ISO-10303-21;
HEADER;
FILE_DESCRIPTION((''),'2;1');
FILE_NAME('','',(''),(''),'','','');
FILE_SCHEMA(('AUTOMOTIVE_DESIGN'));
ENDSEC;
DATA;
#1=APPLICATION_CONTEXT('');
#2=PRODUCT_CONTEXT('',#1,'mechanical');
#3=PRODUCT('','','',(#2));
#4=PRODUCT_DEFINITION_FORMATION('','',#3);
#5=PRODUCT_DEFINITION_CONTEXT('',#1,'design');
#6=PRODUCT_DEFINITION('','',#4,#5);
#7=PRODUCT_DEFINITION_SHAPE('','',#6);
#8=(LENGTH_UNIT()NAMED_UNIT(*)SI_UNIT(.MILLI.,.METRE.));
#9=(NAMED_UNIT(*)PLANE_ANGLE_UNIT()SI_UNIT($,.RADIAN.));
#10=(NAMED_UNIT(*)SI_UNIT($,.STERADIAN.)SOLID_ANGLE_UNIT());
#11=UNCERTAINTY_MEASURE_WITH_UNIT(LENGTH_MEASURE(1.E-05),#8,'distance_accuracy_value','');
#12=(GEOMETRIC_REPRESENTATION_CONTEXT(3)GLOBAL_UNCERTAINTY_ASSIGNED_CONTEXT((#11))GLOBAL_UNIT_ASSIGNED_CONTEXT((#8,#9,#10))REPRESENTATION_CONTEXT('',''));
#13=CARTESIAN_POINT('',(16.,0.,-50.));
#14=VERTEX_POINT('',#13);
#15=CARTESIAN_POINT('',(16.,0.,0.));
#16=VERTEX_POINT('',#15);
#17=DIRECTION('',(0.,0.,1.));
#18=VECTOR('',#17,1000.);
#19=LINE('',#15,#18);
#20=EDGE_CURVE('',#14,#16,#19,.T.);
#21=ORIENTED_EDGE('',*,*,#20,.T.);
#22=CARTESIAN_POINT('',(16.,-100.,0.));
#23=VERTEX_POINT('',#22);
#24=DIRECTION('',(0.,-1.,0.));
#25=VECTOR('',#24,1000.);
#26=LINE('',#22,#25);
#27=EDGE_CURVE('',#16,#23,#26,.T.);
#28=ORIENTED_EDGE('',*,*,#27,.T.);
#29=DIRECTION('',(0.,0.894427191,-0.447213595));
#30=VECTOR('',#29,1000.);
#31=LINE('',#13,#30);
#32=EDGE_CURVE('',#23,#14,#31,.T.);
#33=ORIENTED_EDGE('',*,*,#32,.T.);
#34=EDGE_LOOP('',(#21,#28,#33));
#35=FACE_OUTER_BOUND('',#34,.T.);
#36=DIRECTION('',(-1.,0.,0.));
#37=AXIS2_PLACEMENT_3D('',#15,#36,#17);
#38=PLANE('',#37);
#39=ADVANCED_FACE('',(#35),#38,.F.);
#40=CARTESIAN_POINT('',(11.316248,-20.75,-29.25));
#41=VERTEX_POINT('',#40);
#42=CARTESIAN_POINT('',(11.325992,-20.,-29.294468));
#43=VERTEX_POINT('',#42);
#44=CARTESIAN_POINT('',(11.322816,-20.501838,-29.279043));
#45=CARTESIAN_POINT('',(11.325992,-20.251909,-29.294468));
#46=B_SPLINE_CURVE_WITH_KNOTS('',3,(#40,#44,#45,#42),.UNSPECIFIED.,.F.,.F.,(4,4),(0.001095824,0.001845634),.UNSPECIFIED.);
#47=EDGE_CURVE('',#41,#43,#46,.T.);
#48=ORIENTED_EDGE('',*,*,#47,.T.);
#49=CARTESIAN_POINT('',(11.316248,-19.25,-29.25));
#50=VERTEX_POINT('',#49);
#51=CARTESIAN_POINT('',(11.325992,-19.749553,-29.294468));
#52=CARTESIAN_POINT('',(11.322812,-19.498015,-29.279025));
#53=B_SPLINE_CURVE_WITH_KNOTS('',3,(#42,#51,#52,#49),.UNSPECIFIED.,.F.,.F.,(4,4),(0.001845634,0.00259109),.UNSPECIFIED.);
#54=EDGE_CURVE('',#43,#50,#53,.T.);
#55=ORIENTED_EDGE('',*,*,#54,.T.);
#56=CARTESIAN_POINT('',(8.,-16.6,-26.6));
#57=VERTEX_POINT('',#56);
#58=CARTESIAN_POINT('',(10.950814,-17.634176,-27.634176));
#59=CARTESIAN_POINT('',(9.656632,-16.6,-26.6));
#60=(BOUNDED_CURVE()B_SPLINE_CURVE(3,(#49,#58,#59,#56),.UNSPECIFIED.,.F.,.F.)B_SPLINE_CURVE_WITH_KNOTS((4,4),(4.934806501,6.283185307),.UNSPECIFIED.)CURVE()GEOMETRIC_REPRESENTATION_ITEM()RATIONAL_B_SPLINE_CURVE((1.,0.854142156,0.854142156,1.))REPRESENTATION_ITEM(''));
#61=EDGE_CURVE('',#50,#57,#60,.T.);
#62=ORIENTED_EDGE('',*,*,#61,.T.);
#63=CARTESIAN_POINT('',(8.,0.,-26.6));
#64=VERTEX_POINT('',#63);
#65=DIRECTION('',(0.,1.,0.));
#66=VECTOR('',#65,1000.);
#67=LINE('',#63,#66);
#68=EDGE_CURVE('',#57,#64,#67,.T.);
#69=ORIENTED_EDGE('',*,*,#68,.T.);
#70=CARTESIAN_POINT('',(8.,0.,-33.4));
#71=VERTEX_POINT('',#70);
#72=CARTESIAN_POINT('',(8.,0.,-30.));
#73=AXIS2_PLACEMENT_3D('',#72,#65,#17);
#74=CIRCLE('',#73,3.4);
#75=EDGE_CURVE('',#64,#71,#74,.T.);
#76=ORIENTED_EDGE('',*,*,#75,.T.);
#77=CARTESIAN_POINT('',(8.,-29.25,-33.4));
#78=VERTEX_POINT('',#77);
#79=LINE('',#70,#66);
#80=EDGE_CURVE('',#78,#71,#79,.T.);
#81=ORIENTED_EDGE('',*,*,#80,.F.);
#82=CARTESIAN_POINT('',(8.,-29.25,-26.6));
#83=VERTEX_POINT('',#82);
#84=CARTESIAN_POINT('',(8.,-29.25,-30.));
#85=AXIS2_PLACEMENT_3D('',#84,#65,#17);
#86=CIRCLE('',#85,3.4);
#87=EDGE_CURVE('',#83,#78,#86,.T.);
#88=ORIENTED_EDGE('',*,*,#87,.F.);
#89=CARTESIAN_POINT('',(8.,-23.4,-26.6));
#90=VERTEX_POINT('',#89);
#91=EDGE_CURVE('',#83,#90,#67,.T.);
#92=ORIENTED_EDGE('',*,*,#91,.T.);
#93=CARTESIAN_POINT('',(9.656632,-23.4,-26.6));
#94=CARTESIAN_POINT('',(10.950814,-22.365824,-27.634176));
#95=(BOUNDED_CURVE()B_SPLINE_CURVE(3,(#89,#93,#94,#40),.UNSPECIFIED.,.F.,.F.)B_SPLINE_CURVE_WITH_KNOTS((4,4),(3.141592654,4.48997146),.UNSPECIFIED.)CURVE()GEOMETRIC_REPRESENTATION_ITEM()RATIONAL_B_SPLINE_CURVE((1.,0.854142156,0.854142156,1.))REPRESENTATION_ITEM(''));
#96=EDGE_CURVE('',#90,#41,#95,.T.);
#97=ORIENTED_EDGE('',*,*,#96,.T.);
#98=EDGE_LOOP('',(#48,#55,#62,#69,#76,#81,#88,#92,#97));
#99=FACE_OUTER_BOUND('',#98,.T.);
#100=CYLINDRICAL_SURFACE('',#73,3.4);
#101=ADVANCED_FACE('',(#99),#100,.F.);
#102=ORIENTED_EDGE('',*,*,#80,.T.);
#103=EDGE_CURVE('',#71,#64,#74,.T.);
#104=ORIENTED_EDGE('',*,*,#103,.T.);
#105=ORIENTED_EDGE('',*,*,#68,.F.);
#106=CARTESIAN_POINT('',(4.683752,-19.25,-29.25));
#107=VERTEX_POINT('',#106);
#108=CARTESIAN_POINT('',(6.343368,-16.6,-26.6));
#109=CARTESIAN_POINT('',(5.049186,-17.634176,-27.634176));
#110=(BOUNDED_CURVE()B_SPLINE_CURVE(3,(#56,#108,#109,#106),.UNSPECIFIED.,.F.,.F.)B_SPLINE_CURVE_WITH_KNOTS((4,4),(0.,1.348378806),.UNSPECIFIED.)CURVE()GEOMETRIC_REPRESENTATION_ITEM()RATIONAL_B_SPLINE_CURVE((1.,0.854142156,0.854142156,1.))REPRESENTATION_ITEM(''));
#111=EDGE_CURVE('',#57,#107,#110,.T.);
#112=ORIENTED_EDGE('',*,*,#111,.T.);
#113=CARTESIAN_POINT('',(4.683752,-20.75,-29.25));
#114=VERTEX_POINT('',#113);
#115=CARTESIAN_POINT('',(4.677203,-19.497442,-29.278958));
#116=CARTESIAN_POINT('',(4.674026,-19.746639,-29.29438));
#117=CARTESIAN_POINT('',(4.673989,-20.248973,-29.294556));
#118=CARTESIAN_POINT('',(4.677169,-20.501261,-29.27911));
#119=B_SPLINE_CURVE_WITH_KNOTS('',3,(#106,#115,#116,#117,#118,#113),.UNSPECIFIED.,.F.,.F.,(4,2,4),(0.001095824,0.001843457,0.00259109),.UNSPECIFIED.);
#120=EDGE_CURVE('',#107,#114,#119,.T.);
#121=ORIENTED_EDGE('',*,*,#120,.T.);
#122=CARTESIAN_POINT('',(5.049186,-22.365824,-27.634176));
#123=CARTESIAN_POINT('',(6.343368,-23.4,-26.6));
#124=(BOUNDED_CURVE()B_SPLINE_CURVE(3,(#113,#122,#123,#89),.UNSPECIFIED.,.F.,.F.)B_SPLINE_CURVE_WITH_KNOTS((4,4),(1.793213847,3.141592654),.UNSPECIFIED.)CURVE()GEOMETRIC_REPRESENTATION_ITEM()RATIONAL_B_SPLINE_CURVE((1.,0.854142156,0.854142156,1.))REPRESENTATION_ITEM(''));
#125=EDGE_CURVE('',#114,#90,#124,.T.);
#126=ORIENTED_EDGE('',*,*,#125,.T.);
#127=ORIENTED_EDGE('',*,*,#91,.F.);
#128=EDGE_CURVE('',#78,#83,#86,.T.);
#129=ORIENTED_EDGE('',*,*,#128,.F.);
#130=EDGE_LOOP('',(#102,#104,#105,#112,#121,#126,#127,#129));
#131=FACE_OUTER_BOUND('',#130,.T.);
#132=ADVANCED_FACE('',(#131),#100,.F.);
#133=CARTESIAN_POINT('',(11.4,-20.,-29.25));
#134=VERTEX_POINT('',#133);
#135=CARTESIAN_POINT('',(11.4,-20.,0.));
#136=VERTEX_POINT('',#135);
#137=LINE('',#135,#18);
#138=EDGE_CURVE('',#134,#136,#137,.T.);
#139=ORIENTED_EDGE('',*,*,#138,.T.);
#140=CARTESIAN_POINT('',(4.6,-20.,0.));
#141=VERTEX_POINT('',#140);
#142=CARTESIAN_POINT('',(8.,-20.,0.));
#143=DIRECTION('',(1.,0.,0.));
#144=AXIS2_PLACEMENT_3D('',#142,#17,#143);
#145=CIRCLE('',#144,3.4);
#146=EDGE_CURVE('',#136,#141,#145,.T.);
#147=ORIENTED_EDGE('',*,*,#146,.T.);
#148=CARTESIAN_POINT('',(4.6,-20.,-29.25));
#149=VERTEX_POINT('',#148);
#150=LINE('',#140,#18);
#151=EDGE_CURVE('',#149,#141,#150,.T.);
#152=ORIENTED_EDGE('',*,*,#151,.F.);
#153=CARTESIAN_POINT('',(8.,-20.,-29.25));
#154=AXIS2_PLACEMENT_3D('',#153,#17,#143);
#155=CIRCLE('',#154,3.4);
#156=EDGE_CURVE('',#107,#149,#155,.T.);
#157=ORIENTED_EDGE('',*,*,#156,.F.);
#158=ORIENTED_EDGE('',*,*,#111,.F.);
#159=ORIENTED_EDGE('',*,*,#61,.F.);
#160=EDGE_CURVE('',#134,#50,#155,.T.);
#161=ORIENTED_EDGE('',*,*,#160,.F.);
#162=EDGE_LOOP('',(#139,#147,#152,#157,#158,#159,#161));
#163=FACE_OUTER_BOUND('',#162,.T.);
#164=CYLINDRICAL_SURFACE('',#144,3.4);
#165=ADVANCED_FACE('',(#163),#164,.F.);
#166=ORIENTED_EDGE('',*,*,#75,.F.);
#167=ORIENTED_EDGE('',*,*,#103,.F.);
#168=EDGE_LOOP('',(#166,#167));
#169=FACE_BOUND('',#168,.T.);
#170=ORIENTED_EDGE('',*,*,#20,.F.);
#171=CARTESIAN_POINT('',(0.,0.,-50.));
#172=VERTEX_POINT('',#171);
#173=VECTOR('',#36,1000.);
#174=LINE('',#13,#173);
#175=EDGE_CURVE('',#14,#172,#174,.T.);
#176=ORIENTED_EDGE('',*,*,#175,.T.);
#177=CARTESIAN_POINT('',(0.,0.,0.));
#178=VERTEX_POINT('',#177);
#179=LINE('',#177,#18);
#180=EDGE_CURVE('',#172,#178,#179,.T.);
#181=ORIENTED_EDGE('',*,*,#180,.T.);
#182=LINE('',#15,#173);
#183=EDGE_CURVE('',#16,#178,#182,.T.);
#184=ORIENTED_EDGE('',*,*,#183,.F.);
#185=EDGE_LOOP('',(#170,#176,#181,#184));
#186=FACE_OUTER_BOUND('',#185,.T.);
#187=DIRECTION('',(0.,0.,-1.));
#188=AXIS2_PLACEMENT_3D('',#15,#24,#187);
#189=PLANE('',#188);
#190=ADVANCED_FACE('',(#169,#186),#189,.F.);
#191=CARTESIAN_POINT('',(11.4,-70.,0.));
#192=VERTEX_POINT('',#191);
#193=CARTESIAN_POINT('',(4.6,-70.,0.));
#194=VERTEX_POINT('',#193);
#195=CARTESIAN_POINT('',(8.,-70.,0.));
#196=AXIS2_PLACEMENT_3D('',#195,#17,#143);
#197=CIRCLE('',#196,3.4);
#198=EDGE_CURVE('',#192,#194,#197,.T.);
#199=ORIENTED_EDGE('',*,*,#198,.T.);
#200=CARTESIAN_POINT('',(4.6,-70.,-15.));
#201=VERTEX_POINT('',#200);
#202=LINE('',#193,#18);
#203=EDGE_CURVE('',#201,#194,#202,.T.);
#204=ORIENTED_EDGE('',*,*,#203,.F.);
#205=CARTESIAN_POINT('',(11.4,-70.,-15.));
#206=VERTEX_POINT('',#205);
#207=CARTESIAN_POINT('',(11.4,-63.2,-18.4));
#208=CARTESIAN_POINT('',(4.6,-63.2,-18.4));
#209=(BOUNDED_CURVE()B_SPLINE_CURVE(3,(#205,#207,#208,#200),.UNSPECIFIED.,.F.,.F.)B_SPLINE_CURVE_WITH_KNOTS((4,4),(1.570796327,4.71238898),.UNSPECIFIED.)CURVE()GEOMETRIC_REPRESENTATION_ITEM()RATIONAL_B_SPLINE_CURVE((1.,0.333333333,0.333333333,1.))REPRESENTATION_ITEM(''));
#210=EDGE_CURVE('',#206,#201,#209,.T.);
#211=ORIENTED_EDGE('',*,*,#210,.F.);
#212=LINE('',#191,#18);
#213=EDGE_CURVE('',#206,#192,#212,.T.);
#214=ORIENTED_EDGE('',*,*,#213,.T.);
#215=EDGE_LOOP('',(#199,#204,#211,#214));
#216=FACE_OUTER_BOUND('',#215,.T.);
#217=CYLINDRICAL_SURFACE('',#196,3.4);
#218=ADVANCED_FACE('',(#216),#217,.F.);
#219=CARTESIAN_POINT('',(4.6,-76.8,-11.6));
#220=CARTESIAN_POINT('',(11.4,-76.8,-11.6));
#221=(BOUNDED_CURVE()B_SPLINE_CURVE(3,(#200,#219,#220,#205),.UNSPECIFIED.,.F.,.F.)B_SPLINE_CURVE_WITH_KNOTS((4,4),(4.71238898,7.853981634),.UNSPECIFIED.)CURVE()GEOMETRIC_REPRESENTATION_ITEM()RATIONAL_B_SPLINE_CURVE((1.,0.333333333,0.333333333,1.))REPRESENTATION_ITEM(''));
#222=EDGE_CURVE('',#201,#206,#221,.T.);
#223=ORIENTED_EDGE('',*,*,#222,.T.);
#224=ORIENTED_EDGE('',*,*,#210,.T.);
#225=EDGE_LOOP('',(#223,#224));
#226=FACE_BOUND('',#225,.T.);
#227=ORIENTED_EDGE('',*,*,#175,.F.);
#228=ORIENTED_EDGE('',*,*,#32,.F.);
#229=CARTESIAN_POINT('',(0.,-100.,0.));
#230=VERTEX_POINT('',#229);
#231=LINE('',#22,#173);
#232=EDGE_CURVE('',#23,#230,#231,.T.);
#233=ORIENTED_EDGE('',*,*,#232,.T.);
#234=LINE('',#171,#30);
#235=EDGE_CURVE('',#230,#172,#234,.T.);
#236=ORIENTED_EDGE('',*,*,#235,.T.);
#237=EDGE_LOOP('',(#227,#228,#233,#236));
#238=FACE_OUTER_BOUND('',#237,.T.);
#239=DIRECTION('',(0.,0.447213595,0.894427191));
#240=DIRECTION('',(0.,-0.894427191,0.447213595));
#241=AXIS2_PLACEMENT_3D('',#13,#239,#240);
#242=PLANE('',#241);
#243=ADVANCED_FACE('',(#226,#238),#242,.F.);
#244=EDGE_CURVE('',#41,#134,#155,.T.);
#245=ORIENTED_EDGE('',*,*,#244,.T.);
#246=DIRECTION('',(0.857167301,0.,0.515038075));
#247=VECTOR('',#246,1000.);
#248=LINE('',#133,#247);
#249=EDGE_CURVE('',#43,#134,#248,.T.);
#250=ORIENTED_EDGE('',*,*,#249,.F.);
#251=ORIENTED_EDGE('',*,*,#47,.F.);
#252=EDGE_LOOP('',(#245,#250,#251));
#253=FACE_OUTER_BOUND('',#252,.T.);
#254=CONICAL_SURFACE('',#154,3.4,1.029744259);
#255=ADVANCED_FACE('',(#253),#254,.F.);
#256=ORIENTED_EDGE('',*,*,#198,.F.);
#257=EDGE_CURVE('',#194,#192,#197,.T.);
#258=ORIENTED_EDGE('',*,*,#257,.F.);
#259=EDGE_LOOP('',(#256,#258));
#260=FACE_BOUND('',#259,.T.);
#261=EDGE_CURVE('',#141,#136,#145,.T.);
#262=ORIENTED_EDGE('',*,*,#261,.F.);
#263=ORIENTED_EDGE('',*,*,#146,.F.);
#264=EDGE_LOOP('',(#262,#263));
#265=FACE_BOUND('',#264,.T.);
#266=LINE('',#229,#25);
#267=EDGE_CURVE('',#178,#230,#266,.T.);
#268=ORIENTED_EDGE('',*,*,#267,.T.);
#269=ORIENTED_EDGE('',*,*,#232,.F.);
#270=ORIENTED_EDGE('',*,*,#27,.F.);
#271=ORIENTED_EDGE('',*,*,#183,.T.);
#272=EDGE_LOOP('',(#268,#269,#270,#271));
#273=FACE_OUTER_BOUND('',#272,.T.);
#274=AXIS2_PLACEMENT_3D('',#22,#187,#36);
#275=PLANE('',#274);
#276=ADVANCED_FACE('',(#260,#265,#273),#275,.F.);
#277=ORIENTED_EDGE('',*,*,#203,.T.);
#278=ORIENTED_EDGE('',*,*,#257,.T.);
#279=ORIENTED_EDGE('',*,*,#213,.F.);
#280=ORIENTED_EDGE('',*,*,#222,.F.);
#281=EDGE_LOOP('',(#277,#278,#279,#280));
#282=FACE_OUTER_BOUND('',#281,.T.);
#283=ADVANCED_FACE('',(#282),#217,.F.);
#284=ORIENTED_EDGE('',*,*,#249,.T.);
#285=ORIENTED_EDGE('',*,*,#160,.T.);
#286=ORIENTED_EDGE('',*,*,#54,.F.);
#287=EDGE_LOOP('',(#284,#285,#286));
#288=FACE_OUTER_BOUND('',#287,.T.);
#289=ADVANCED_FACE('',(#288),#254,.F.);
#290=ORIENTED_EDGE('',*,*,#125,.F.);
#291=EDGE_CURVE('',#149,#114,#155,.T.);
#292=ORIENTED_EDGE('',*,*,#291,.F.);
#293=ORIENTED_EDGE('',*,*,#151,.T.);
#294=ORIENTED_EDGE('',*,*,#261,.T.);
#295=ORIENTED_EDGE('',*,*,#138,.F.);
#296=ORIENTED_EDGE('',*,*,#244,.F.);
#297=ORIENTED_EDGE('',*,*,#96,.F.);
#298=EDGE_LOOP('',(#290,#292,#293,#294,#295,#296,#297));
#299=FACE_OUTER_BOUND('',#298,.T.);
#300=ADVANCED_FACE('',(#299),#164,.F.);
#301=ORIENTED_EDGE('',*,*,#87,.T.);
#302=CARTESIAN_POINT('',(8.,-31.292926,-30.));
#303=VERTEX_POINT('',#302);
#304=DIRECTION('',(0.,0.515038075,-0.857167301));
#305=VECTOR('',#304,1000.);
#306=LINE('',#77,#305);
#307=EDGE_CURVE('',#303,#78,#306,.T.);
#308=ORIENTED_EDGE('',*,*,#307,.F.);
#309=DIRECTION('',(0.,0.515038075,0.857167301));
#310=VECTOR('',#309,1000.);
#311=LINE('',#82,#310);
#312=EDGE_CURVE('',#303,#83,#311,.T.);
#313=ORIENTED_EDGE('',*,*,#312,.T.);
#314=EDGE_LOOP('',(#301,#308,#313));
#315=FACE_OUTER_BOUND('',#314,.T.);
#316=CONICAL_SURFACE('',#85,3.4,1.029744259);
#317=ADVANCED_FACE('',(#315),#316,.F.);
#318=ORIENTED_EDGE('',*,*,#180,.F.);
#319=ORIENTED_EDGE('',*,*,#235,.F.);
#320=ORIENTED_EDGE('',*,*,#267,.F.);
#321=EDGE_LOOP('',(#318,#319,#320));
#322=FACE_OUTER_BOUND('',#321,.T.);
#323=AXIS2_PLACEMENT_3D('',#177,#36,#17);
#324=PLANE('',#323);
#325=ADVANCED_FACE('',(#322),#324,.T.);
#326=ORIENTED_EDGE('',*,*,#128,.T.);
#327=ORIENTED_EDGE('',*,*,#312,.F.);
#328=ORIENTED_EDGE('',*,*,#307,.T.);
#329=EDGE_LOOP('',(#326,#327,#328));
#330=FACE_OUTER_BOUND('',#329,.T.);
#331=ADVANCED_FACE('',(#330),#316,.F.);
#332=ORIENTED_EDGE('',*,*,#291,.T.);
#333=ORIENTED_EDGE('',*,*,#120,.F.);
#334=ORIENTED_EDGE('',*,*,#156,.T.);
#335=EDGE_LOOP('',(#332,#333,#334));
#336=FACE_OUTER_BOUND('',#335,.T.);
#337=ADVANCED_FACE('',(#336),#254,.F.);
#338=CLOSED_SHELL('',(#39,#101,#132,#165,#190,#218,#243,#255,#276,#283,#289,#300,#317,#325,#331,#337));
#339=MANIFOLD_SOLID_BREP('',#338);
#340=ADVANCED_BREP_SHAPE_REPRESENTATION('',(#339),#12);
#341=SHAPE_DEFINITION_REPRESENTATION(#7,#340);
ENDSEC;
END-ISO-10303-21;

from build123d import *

# Parameters (mm, degrees)
EXTRUDE_1_DEPTH        = 16
HOLE_WIZARD_M8_1_D     = 6.8
HOLE_WIZARD_M8_1_DEPTH = 29.25
HOLE_WIZARD_M8_1_TIP   = 2.042926105
HOLE_WIZARD_M8_2_D     = 6.8
HOLE_WIZARD_M8_2_DEPTH = 29.25
HOLE_WIZARD_M8_2_TIP   = 2.042926105


with BuildPart() as part:
    # 草图1 → 凸台-拉伸1 (new body)
    with BuildSketch(Plane(origin=(0, 0, 0), x_dir=(0, 0, -1), z_dir=(1, 0, 0))):
        Polygon((0, 0), (50, 0), (0, -100), align=None)
    extrude(amount=EXTRUDE_1_DEPTH)

    # M8 螺纹孔1
    with Locations(Plane(origin=(0, 0, 0), x_dir=(1, 0, 0), z_dir=(0, 1, 0))):
        with Locations((8, 30)):
            Hole(HOLE_WIZARD_M8_1_D / 2, depth=HOLE_WIZARD_M8_1_DEPTH)
            with Locations((0, 0, -(HOLE_WIZARD_M8_1_DEPTH + HOLE_WIZARD_M8_1_TIP / 2))):  # 118° drill point
                Cone(0, HOLE_WIZARD_M8_1_D / 2, HOLE_WIZARD_M8_1_TIP, mode=Mode.SUBTRACT)

    # M8 螺纹孔2
    with Locations(Plane.XY):
        with Locations((8, -20), (8, -70)):
            Hole(HOLE_WIZARD_M8_2_D / 2, depth=HOLE_WIZARD_M8_2_DEPTH)
            with Locations((0, 0, -(HOLE_WIZARD_M8_2_DEPTH + HOLE_WIZARD_M8_2_TIP / 2))):  # 118° drill point
                Cone(0, HOLE_WIZARD_M8_2_D / 2, HOLE_WIZARD_M8_2_TIP, mode=Mode.SUBTRACT)


solid = part.part
